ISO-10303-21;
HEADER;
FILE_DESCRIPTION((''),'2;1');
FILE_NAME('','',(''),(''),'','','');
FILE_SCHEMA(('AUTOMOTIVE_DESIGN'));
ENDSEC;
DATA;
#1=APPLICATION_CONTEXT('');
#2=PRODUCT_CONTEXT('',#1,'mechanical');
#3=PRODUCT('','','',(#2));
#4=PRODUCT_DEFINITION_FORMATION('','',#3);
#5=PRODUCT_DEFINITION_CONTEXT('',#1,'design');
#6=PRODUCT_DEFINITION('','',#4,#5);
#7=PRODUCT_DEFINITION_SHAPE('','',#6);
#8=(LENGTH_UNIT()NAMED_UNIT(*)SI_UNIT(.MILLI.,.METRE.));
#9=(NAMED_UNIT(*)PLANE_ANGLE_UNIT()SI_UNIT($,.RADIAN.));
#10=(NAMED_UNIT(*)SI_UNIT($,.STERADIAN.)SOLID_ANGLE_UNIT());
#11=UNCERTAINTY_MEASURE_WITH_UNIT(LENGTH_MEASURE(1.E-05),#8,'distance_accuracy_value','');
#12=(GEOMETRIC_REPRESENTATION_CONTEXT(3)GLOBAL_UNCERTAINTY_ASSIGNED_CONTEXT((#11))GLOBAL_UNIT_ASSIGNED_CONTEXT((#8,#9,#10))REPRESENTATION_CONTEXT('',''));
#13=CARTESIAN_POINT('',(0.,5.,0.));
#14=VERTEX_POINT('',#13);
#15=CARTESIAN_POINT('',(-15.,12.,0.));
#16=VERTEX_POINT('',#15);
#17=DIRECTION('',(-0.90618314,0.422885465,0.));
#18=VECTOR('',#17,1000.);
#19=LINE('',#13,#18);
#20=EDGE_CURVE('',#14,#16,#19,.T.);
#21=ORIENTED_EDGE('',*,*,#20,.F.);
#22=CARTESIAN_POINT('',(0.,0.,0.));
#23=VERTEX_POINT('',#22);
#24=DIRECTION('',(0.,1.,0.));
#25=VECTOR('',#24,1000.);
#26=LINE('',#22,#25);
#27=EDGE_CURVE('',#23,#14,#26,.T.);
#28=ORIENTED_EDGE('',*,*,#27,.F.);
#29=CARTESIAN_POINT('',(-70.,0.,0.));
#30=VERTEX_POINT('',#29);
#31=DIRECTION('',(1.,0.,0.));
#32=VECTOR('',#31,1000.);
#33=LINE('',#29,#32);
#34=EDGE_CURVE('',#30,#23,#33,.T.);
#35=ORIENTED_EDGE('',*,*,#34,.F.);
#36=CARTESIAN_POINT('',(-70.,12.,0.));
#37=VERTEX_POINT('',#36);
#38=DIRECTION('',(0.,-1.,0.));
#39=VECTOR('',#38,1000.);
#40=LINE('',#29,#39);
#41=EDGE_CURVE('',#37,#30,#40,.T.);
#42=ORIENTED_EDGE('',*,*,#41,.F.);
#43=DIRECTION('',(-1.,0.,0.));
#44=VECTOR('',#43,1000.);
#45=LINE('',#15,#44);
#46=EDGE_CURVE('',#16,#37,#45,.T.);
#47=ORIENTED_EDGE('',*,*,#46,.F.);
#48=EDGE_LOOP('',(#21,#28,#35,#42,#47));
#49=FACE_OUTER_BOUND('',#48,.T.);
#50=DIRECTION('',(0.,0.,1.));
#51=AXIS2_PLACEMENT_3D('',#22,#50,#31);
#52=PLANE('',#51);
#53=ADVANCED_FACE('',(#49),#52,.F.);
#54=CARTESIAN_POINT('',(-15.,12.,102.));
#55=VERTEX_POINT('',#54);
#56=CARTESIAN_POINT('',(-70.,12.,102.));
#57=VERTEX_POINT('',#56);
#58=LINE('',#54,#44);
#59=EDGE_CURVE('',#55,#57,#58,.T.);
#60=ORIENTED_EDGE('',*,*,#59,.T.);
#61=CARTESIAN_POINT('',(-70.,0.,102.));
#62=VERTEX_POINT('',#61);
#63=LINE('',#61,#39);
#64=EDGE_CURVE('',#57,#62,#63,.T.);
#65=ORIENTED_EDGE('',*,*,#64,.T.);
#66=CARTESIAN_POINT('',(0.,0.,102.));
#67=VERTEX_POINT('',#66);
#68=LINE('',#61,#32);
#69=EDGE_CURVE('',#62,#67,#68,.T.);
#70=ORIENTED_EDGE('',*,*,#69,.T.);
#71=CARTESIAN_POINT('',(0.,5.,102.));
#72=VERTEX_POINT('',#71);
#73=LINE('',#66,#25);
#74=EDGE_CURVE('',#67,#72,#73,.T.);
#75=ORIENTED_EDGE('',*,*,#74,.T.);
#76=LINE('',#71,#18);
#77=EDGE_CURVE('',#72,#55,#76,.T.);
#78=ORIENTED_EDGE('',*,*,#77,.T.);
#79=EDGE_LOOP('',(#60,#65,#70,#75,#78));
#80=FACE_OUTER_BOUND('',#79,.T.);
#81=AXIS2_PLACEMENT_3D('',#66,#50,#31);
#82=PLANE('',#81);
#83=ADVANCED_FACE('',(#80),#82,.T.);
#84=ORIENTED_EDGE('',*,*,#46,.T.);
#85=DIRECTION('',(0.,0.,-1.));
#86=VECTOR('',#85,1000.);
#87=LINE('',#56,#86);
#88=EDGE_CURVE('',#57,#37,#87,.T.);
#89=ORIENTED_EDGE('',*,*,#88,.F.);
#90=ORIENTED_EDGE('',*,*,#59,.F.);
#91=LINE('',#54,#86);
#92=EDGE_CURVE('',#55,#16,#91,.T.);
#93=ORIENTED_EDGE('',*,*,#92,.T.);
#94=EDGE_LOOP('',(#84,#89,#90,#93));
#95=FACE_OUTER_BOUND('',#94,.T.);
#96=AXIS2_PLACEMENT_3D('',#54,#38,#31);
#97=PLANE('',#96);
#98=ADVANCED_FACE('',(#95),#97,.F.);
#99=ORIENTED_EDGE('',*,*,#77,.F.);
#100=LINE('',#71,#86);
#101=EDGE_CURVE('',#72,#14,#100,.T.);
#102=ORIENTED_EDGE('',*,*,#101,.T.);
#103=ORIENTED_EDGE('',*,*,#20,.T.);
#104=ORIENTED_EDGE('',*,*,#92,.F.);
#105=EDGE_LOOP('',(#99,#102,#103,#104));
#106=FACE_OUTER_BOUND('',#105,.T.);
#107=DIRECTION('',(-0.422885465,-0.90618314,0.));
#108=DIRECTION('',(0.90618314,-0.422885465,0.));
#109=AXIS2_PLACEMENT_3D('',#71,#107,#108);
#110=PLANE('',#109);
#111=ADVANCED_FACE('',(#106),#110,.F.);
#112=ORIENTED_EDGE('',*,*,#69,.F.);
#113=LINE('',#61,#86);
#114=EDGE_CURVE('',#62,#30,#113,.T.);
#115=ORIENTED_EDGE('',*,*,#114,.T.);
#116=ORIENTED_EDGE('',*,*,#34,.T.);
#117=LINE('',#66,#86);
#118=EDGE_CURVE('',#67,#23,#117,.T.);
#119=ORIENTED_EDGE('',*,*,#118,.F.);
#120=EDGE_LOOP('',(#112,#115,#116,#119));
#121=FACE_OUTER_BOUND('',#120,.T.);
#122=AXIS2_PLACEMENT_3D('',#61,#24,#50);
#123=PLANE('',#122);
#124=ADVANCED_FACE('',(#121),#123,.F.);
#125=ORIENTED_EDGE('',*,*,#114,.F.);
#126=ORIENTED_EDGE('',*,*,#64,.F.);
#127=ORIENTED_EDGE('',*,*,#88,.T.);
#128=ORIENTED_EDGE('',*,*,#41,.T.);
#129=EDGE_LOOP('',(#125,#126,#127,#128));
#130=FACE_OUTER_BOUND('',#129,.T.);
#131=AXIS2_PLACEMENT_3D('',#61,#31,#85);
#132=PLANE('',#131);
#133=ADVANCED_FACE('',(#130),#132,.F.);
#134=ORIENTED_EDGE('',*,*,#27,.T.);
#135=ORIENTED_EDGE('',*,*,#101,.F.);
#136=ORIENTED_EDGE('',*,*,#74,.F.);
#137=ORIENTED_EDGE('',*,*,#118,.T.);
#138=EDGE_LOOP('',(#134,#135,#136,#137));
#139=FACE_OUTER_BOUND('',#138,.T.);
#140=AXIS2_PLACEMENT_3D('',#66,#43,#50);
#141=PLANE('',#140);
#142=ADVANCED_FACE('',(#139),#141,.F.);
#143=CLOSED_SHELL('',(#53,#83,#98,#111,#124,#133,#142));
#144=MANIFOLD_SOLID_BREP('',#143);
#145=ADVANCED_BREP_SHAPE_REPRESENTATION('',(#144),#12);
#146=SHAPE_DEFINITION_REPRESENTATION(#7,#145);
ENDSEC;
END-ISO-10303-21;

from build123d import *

# Parameters (mm, degrees)
BOSS_EXTRUDE1_DEPTH = 102


with BuildPart() as part:
    # Sketch1 → Boss-Extrude1 (new body)
    with BuildSketch(Plane.XY):
        Polygon((0, 0), (0, 5), (-15, 12), (-70, 12), (-70, 0), align=None)
    extrude(amount=BOSS_EXTRUDE1_DEPTH)


solid = part.part
